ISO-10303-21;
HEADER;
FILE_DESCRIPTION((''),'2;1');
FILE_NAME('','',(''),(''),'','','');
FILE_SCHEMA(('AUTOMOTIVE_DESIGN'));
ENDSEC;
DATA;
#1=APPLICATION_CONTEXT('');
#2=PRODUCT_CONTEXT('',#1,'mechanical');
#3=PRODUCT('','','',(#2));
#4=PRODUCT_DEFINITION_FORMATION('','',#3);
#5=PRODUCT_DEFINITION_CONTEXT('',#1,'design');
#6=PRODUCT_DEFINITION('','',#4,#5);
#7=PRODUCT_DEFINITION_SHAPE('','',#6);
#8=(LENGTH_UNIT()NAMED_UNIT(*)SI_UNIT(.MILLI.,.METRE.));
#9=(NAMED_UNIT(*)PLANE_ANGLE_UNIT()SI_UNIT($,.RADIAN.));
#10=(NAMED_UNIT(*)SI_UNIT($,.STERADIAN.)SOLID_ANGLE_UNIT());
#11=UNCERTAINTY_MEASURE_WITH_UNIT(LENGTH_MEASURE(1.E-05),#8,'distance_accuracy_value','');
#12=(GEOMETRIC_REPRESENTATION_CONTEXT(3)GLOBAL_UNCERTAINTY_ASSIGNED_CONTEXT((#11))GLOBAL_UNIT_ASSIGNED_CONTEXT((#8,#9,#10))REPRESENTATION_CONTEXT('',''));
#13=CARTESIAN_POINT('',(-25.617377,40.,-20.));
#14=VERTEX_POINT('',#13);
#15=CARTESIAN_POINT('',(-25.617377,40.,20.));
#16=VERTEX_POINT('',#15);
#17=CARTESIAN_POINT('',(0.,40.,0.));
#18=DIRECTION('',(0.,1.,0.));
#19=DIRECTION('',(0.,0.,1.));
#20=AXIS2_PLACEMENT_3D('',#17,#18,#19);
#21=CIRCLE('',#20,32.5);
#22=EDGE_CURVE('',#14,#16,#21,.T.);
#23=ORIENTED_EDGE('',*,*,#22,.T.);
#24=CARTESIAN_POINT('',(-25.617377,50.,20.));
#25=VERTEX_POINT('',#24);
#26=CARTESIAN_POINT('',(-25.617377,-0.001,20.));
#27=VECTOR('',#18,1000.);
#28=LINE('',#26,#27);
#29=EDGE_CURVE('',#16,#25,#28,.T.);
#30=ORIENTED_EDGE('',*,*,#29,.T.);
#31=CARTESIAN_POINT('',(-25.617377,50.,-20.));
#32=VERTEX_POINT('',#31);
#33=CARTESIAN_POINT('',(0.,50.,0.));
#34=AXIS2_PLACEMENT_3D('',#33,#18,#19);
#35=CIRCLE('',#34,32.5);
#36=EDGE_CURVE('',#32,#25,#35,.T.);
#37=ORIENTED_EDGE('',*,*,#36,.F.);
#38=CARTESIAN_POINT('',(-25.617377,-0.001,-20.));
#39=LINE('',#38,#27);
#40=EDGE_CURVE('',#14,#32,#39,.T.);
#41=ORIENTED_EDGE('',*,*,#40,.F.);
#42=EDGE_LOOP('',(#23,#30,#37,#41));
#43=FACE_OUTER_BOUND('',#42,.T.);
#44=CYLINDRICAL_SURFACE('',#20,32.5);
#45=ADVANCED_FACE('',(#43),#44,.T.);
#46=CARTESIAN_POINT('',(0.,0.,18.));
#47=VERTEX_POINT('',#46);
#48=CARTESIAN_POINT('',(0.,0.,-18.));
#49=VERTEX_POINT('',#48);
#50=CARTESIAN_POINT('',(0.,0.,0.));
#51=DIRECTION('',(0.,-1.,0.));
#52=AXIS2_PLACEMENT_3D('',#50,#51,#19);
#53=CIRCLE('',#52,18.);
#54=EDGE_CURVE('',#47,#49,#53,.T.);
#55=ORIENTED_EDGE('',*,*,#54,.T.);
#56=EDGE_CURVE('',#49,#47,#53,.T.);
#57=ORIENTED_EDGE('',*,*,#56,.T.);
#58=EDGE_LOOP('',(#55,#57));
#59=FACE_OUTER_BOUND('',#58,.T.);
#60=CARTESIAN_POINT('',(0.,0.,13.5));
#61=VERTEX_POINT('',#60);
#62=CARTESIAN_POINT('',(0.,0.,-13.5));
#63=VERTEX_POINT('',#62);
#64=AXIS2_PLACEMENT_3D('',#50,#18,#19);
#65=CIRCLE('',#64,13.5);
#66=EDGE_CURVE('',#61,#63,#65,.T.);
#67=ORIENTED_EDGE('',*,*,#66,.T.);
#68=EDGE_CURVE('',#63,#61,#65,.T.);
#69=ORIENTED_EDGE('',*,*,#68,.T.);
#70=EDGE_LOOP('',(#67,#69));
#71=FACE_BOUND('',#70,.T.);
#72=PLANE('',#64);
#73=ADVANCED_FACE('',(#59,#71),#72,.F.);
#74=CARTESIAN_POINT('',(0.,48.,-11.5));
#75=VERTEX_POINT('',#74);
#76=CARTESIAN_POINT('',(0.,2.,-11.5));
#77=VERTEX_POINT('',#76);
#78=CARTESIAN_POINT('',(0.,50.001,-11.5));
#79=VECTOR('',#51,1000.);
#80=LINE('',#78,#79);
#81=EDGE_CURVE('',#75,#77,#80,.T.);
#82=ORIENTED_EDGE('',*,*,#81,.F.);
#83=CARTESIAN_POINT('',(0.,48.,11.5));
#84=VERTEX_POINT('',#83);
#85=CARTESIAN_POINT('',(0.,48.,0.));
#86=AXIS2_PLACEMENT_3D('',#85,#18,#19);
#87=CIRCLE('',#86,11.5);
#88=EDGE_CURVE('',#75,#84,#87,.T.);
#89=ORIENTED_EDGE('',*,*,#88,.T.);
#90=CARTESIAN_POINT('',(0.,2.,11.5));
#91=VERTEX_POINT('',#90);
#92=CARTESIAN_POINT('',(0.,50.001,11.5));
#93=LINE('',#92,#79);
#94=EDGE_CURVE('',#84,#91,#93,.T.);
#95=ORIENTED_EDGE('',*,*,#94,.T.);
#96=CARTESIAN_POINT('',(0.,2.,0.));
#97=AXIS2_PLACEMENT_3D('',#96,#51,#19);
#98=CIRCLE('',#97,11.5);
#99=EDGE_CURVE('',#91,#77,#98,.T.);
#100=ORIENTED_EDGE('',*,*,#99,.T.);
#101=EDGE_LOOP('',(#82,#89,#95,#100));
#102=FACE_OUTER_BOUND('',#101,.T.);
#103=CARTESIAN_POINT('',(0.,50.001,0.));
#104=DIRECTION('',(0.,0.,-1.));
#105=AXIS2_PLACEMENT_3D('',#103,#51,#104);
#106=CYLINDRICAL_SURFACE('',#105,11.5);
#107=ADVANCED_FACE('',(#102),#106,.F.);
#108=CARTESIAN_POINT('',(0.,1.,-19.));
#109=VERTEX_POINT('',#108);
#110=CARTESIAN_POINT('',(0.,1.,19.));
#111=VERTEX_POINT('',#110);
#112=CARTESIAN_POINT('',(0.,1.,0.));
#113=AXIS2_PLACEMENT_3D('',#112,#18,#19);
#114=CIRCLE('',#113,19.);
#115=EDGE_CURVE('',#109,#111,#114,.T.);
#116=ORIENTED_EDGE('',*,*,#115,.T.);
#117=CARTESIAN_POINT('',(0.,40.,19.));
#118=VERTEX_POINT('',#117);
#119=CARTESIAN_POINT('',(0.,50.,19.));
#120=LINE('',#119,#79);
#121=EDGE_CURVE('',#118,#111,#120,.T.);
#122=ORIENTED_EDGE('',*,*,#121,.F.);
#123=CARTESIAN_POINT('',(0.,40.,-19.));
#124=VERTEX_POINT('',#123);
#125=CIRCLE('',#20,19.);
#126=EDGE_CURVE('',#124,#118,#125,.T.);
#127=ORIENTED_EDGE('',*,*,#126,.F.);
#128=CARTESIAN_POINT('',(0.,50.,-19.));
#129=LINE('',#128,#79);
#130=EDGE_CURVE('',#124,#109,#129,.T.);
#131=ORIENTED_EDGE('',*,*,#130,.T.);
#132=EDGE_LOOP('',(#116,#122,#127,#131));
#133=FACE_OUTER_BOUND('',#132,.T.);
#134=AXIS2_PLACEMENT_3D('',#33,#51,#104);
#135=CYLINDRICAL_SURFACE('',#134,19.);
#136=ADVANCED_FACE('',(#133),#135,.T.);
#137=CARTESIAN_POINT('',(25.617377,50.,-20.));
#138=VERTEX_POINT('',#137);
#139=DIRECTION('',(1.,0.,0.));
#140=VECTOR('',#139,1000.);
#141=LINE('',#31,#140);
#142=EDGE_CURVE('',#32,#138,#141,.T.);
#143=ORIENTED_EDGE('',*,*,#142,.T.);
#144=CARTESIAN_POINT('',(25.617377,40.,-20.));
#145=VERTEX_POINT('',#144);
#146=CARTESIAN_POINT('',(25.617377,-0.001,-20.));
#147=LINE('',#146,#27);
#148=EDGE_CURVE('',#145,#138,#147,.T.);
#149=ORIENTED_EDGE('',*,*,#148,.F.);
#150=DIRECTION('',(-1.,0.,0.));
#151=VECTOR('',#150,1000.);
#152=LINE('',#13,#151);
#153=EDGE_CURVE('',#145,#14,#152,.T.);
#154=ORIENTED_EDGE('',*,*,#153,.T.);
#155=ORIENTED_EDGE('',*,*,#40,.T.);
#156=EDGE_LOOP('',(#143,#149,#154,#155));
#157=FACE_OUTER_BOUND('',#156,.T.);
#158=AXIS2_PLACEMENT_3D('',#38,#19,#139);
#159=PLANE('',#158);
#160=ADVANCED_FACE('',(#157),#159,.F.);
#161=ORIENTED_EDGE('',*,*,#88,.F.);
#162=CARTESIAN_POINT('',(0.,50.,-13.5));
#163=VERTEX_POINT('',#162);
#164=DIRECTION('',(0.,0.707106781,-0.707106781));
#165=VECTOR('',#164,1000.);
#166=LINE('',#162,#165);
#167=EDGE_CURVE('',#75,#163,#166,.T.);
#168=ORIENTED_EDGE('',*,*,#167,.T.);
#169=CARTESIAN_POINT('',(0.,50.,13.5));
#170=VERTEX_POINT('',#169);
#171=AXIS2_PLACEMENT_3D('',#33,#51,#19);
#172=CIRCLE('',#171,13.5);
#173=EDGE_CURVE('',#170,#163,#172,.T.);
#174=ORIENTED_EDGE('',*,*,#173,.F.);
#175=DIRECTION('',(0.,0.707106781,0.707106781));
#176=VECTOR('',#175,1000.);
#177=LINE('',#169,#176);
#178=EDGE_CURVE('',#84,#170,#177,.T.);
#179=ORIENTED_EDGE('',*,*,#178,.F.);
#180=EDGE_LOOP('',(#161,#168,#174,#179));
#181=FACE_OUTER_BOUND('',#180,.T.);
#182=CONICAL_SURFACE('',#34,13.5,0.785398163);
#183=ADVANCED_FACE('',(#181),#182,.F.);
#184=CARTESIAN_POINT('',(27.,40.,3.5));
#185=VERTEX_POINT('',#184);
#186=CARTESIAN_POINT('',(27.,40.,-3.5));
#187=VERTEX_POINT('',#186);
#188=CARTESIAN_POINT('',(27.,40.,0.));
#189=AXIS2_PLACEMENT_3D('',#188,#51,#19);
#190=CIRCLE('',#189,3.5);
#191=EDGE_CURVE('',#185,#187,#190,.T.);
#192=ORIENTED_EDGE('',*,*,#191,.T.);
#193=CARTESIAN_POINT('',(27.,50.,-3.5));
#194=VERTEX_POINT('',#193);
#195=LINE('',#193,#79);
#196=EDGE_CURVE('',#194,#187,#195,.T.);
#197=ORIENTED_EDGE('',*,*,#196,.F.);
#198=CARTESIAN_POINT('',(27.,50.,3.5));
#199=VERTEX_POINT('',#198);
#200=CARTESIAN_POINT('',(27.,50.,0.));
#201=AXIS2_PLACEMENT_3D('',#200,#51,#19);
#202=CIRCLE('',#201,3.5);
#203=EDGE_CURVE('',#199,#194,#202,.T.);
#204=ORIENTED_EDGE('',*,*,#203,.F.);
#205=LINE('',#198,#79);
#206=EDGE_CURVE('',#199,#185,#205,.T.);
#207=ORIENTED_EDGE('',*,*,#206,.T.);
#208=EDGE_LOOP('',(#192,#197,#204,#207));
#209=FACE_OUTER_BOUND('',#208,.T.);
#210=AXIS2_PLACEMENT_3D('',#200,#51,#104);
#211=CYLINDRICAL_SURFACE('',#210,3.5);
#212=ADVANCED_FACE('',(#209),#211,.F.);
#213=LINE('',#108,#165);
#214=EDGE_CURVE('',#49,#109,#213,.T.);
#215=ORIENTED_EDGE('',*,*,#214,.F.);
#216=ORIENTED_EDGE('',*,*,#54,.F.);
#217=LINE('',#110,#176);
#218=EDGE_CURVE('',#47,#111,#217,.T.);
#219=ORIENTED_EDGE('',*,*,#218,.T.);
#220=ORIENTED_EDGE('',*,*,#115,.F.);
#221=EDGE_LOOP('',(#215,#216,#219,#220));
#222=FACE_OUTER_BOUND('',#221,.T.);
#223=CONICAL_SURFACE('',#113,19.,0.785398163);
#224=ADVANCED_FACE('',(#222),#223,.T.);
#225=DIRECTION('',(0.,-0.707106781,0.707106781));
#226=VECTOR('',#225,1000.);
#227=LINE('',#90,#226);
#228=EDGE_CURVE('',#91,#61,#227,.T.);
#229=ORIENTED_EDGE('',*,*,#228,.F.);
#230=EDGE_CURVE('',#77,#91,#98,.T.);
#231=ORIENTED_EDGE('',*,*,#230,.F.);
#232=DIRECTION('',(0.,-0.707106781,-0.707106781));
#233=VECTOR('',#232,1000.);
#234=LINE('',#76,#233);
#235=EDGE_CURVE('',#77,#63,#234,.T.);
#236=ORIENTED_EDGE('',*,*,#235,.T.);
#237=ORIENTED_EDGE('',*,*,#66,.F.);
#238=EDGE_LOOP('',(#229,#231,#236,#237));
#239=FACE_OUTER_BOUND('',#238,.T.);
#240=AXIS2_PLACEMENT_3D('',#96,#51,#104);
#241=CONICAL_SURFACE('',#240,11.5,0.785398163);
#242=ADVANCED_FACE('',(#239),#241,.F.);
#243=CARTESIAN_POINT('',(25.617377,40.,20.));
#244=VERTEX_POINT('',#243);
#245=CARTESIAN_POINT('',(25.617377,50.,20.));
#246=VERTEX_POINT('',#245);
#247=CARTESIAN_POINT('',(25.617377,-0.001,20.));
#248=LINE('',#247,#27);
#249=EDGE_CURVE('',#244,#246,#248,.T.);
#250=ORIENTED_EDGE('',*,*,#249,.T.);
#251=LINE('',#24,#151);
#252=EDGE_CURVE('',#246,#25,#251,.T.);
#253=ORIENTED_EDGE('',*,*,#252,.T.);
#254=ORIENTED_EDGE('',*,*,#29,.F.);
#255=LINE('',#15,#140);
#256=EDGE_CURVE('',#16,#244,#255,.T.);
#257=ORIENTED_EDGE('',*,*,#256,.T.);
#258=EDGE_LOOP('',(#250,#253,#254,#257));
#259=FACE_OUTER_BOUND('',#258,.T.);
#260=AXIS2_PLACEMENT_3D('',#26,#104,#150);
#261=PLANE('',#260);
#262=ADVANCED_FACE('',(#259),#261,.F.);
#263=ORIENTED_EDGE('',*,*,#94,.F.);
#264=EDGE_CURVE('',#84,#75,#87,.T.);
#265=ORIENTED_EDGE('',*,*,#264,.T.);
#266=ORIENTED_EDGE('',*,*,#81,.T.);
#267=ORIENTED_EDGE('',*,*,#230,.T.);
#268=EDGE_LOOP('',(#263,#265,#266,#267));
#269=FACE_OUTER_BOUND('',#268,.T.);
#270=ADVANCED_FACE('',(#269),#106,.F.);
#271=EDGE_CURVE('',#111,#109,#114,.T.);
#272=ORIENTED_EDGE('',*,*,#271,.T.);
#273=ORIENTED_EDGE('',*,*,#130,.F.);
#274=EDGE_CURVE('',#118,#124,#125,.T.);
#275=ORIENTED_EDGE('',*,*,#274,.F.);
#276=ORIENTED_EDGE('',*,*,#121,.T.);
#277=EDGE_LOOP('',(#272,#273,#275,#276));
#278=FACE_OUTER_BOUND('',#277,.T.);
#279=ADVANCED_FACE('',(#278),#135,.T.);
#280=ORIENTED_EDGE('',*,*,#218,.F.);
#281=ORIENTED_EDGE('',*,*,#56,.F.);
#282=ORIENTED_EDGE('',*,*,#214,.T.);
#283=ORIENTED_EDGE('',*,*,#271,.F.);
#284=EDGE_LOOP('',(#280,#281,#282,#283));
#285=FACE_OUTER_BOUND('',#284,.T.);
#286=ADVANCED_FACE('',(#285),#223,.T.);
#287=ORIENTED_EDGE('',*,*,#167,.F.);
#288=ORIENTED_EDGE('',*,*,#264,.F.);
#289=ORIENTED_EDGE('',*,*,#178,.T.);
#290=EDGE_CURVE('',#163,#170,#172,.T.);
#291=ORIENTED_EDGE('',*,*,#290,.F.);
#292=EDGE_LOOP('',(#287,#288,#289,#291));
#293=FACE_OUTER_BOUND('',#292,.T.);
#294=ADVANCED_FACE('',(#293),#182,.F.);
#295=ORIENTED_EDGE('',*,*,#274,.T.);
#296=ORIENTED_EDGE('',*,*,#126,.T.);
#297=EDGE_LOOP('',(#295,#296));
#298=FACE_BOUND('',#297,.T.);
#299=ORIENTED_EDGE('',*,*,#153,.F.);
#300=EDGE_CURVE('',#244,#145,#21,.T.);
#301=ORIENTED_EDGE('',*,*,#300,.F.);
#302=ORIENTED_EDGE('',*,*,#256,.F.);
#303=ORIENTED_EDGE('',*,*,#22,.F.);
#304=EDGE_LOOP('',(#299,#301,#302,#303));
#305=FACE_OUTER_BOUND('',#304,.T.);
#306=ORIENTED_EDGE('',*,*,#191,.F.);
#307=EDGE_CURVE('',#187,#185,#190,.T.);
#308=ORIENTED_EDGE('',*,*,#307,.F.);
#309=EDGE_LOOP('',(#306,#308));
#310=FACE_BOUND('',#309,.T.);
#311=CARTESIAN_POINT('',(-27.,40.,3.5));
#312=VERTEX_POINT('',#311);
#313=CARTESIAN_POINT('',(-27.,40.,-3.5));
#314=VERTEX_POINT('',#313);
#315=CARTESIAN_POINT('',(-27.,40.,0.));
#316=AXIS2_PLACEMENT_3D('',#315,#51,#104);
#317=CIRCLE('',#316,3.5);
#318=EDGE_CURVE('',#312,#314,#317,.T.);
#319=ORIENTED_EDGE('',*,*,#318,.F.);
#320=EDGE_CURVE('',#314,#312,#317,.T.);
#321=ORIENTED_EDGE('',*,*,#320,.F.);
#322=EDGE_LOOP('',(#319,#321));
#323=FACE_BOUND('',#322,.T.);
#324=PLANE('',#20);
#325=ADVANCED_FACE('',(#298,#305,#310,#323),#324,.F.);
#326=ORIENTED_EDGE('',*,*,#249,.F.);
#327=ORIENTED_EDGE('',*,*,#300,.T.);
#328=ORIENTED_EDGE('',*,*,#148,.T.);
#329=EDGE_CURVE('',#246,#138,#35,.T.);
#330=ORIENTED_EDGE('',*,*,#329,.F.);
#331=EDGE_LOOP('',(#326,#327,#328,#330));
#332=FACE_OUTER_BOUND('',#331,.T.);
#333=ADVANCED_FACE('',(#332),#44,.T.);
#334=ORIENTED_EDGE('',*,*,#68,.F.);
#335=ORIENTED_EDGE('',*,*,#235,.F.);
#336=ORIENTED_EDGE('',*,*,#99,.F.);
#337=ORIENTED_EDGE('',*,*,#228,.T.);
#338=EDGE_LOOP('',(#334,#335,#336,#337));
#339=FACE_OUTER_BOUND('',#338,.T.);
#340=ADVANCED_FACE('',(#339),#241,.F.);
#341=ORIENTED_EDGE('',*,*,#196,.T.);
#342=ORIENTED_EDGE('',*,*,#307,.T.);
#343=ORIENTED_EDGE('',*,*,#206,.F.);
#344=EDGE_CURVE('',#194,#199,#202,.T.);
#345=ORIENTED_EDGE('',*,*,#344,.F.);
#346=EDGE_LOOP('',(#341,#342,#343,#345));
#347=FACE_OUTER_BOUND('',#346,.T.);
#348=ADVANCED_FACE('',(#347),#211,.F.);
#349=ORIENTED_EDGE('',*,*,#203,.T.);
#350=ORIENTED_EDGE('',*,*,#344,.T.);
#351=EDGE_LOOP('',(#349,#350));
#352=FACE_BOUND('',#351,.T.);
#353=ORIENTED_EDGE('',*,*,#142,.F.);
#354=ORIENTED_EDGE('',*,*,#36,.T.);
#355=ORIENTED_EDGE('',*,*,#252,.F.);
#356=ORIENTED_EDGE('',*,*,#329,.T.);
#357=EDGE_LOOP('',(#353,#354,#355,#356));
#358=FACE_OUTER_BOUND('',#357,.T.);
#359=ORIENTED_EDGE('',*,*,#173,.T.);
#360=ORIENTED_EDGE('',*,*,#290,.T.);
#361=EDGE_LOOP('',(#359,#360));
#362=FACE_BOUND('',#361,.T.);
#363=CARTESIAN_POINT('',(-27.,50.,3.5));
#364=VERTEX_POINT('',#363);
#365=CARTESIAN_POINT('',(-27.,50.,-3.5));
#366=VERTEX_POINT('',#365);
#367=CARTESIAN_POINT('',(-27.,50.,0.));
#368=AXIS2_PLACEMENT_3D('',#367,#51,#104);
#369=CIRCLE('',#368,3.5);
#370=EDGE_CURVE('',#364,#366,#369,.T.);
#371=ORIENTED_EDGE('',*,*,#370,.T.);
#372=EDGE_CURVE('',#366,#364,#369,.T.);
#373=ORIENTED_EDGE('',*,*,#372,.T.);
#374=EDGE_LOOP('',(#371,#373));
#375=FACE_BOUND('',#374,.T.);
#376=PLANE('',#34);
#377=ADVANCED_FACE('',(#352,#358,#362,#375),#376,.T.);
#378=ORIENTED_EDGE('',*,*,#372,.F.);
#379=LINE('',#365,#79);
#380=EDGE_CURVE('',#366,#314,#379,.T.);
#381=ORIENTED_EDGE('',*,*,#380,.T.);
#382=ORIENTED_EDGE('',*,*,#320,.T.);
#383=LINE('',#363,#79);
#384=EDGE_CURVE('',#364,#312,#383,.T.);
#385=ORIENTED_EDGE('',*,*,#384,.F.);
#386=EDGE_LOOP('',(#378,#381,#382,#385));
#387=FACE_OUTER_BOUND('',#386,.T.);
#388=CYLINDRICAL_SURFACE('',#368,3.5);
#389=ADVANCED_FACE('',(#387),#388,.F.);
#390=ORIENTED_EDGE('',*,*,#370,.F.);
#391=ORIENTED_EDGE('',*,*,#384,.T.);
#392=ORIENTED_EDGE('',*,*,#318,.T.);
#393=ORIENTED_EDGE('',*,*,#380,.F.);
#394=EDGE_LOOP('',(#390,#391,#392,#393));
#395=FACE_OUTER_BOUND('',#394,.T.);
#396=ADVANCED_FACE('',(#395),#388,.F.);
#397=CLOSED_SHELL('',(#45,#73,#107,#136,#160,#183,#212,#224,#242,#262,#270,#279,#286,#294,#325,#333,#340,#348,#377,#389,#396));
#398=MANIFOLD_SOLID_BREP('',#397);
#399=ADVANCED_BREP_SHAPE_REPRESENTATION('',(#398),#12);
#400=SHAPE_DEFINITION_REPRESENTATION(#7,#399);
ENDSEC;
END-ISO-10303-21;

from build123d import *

# Parameters (mm, degrees)
SKETCH1_R           = 19
BOSS_EXTRUDE1_DEPTH = 50
SKETCH2_R           = 32.5
BOSS_EXTRUDE2_DEPTH = 10
CUT_EXTRUDE1_REACH  = 69.915
SKETCH3_R           = 11.5
SKETCH4_R           = 3.5
CUT_EXTRUDE2_DEPTH  = 61.930288035
CIRPATTERN1_COUNT   = 4
CHAMFER1_SIZE       = 1
CHAMFER2_SIZE       = 2
CUT_EXTRUDE3_REACH  = 69.915


with BuildPart() as part:
    # Sketch1 → Boss-Extrude1 (new body)
    with BuildSketch(Plane(origin=(0, 0, 0), x_dir=(1, 0, 0), z_dir=(0, 1, 0))):
        with Locations(Location((0, 0, 0), (0, 0, 270))):
            Circle(SKETCH1_R)
    extrude(amount=BOSS_EXTRUDE1_DEPTH)

    # Sketch2 → Boss-Extrude2 (add)
    with BuildSketch(Plane(origin=(0, 50, 0), x_dir=(1, 0, 0), z_dir=(0, 1, 0))):
        with Locations(Location((0, 0, 0), (0, 0, 270))):
            Circle(SKETCH2_R)
    extrude(amount=-BOSS_EXTRUDE2_DEPTH)

    # Sketch3 → Cut-Extrude1 (cut, up to next)
    with BuildSketch(Plane.XZ, mode=Mode.PRIVATE) as cut_extrude1_sk1:
        with Locations(Location((0, 0, 0), (0, 0, 270))):
            Circle(SKETCH3_R)
    cut_extrude1_tool1 = extrude(cut_extrude1_sk1.sketch, amount=-CUT_EXTRUDE1_REACH, mode=Mode.PRIVATE) & part.part
    cut_extrude1 = cut_extrude1_tool1.solids().sort_by_distance((0, 0, 0))[0]
    add(cut_extrude1, mode=Mode.SUBTRACT)

    # Sketch4 → Cut-Extrude2 (cut, through all)
    with BuildSketch(Plane.XZ.offset(-40)):
        with Locations(Location((-27, 0, 0), (0, 0, 270))):
            Circle(SKETCH4_R)
    cut_extrude2 = extrude(amount=-CUT_EXTRUDE2_DEPTH, mode=Mode.SUBTRACT)

    # CirPattern1: Cut-Extrude1, Cut-Extrude2 ×4 about axis
    cirpattern1_axis = Axis((0, 0, 0), (0, 1, 0))
    add([cut_extrude1.rotate(cirpattern1_axis, i * 360 / CIRPATTERN1_COUNT) for i in range(1, CIRPATTERN1_COUNT)], mode=Mode.SUBTRACT)
    add([cut_extrude2.rotate(cirpattern1_axis, i * 360 / CIRPATTERN1_COUNT) for i in range(1, CIRPATTERN1_COUNT)], mode=Mode.SUBTRACT)

    # Chamfer1
    chamfer1_edges = [part.edges().sort_by_distance(p)[0] for p in [
        (0, 0, -19),
    ]]
    chamfer(chamfer1_edges, length=CHAMFER1_SIZE)

    # Chamfer2
    chamfer2_edges = [part.edges().sort_by_distance(p)[0] for p in [
        (0, 50, 11.5),
        (0, 0, 11.5),
    ]]
    chamfer(chamfer2_edges, length=CHAMFER2_SIZE)

    # Sketch5 → Cut-Extrude3 (cut, up to next)
    with BuildSketch(Plane(origin=(0, 50, 0), x_dir=(1, 0, 0), z_dir=(0, 1, 0)), mode=Mode.PRIVATE) as cut_extrude3_sk1:
        with BuildLine():
            Line((-25.617376915, -20), (25.617376915, -20))
            ThreePointArc((25.617376915, -20), (0, -32.5), (-25.617376915, -20))
        make_face()
    cut_extrude3_tool1 = extrude(cut_extrude3_sk1.sketch, amount=-CUT_EXTRUDE3_REACH, mode=Mode.PRIVATE) & part.part
    # Sketch5 → Cut-Extrude3 (cut, up to next)
    with BuildSketch(Plane(origin=(0, 50, 0), x_dir=(1, 0, 0), z_dir=(0, 1, 0)), mode=Mode.PRIVATE) as cut_extrude3_sk2:
        with BuildLine():
            Line((-25.617376915, 20), (25.617376915, 20))
            ThreePointArc((25.617376915, 20), (0, 32.5), (-25.617376915, 20))
        make_face()
    cut_extrude3_tool2 = extrude(cut_extrude3_sk2.sketch, amount=-CUT_EXTRUDE3_REACH, mode=Mode.PRIVATE) & part.part
    add(cut_extrude3_tool1.solids().sort_by_distance((0, 50, 25.09283))[0], mode=Mode.SUBTRACT)
    add(cut_extrude3_tool2.solids().sort_by_distance((0, 50, -25.09283))[0], mode=Mode.SUBTRACT)


solid = part.part
